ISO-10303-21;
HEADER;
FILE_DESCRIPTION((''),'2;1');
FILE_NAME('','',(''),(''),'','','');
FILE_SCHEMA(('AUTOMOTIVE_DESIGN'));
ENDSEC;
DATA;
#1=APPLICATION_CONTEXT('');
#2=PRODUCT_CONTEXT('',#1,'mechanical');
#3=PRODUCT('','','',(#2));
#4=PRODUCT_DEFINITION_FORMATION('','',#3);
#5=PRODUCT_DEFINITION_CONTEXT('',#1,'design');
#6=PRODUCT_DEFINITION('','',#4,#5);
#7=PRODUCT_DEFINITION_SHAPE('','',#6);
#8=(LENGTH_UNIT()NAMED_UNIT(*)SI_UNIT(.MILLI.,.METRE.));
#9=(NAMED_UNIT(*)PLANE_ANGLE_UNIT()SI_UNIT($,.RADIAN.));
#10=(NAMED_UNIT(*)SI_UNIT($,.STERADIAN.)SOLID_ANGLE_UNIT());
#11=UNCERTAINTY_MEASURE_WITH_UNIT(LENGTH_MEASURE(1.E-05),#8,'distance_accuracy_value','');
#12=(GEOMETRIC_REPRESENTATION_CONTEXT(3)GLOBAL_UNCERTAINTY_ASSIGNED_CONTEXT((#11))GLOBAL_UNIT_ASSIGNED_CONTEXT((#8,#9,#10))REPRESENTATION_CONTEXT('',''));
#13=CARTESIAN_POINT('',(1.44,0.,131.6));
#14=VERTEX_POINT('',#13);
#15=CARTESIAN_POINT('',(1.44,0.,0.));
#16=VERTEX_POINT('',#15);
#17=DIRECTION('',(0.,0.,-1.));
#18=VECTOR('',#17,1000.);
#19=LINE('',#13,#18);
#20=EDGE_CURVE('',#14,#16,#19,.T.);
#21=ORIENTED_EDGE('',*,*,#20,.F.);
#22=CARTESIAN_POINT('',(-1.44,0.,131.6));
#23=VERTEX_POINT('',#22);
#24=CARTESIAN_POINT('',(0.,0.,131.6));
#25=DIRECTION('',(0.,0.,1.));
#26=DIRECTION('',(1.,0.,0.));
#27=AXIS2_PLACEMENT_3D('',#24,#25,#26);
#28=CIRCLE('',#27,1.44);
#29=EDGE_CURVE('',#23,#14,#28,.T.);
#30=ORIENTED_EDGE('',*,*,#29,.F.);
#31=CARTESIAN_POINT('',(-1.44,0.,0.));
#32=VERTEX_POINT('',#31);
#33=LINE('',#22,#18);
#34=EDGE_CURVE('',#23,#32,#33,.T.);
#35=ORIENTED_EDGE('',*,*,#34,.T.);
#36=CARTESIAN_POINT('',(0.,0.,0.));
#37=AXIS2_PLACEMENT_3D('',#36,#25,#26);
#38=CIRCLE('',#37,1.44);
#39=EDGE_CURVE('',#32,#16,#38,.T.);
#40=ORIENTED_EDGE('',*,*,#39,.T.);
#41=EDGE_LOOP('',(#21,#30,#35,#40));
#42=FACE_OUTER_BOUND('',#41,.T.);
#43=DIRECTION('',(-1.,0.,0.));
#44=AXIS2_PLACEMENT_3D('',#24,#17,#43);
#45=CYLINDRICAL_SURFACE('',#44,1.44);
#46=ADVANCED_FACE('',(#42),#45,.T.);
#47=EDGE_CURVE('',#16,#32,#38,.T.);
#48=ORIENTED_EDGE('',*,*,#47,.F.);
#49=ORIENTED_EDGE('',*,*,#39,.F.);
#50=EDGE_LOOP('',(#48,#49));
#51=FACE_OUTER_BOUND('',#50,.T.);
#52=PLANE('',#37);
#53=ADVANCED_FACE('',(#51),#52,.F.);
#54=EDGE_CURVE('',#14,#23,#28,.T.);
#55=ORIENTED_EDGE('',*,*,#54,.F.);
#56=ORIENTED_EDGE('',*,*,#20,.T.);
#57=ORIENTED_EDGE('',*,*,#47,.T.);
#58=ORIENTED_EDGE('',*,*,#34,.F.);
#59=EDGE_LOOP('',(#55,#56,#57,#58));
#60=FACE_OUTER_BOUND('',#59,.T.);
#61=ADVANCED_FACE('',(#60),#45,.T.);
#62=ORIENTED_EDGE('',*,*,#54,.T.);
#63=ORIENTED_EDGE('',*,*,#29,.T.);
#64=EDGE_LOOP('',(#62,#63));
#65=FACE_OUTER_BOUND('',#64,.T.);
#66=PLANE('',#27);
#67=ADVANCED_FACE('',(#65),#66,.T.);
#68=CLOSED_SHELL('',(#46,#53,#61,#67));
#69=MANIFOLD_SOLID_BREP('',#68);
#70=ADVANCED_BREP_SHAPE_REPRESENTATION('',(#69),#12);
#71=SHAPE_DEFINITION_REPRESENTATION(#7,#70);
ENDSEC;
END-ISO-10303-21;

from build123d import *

# Parameters (mm, degrees)
SKETCH1_R           = 1.44
BOSS_EXTRUDE1_DEPTH = 131.6


with BuildPart() as part:
    # Sketch1 → Boss-Extrude1 (new body)
    with BuildSketch(Plane.XY):
        Circle(SKETCH1_R)
    extrude(amount=BOSS_EXTRUDE1_DEPTH)


solid = part.part
